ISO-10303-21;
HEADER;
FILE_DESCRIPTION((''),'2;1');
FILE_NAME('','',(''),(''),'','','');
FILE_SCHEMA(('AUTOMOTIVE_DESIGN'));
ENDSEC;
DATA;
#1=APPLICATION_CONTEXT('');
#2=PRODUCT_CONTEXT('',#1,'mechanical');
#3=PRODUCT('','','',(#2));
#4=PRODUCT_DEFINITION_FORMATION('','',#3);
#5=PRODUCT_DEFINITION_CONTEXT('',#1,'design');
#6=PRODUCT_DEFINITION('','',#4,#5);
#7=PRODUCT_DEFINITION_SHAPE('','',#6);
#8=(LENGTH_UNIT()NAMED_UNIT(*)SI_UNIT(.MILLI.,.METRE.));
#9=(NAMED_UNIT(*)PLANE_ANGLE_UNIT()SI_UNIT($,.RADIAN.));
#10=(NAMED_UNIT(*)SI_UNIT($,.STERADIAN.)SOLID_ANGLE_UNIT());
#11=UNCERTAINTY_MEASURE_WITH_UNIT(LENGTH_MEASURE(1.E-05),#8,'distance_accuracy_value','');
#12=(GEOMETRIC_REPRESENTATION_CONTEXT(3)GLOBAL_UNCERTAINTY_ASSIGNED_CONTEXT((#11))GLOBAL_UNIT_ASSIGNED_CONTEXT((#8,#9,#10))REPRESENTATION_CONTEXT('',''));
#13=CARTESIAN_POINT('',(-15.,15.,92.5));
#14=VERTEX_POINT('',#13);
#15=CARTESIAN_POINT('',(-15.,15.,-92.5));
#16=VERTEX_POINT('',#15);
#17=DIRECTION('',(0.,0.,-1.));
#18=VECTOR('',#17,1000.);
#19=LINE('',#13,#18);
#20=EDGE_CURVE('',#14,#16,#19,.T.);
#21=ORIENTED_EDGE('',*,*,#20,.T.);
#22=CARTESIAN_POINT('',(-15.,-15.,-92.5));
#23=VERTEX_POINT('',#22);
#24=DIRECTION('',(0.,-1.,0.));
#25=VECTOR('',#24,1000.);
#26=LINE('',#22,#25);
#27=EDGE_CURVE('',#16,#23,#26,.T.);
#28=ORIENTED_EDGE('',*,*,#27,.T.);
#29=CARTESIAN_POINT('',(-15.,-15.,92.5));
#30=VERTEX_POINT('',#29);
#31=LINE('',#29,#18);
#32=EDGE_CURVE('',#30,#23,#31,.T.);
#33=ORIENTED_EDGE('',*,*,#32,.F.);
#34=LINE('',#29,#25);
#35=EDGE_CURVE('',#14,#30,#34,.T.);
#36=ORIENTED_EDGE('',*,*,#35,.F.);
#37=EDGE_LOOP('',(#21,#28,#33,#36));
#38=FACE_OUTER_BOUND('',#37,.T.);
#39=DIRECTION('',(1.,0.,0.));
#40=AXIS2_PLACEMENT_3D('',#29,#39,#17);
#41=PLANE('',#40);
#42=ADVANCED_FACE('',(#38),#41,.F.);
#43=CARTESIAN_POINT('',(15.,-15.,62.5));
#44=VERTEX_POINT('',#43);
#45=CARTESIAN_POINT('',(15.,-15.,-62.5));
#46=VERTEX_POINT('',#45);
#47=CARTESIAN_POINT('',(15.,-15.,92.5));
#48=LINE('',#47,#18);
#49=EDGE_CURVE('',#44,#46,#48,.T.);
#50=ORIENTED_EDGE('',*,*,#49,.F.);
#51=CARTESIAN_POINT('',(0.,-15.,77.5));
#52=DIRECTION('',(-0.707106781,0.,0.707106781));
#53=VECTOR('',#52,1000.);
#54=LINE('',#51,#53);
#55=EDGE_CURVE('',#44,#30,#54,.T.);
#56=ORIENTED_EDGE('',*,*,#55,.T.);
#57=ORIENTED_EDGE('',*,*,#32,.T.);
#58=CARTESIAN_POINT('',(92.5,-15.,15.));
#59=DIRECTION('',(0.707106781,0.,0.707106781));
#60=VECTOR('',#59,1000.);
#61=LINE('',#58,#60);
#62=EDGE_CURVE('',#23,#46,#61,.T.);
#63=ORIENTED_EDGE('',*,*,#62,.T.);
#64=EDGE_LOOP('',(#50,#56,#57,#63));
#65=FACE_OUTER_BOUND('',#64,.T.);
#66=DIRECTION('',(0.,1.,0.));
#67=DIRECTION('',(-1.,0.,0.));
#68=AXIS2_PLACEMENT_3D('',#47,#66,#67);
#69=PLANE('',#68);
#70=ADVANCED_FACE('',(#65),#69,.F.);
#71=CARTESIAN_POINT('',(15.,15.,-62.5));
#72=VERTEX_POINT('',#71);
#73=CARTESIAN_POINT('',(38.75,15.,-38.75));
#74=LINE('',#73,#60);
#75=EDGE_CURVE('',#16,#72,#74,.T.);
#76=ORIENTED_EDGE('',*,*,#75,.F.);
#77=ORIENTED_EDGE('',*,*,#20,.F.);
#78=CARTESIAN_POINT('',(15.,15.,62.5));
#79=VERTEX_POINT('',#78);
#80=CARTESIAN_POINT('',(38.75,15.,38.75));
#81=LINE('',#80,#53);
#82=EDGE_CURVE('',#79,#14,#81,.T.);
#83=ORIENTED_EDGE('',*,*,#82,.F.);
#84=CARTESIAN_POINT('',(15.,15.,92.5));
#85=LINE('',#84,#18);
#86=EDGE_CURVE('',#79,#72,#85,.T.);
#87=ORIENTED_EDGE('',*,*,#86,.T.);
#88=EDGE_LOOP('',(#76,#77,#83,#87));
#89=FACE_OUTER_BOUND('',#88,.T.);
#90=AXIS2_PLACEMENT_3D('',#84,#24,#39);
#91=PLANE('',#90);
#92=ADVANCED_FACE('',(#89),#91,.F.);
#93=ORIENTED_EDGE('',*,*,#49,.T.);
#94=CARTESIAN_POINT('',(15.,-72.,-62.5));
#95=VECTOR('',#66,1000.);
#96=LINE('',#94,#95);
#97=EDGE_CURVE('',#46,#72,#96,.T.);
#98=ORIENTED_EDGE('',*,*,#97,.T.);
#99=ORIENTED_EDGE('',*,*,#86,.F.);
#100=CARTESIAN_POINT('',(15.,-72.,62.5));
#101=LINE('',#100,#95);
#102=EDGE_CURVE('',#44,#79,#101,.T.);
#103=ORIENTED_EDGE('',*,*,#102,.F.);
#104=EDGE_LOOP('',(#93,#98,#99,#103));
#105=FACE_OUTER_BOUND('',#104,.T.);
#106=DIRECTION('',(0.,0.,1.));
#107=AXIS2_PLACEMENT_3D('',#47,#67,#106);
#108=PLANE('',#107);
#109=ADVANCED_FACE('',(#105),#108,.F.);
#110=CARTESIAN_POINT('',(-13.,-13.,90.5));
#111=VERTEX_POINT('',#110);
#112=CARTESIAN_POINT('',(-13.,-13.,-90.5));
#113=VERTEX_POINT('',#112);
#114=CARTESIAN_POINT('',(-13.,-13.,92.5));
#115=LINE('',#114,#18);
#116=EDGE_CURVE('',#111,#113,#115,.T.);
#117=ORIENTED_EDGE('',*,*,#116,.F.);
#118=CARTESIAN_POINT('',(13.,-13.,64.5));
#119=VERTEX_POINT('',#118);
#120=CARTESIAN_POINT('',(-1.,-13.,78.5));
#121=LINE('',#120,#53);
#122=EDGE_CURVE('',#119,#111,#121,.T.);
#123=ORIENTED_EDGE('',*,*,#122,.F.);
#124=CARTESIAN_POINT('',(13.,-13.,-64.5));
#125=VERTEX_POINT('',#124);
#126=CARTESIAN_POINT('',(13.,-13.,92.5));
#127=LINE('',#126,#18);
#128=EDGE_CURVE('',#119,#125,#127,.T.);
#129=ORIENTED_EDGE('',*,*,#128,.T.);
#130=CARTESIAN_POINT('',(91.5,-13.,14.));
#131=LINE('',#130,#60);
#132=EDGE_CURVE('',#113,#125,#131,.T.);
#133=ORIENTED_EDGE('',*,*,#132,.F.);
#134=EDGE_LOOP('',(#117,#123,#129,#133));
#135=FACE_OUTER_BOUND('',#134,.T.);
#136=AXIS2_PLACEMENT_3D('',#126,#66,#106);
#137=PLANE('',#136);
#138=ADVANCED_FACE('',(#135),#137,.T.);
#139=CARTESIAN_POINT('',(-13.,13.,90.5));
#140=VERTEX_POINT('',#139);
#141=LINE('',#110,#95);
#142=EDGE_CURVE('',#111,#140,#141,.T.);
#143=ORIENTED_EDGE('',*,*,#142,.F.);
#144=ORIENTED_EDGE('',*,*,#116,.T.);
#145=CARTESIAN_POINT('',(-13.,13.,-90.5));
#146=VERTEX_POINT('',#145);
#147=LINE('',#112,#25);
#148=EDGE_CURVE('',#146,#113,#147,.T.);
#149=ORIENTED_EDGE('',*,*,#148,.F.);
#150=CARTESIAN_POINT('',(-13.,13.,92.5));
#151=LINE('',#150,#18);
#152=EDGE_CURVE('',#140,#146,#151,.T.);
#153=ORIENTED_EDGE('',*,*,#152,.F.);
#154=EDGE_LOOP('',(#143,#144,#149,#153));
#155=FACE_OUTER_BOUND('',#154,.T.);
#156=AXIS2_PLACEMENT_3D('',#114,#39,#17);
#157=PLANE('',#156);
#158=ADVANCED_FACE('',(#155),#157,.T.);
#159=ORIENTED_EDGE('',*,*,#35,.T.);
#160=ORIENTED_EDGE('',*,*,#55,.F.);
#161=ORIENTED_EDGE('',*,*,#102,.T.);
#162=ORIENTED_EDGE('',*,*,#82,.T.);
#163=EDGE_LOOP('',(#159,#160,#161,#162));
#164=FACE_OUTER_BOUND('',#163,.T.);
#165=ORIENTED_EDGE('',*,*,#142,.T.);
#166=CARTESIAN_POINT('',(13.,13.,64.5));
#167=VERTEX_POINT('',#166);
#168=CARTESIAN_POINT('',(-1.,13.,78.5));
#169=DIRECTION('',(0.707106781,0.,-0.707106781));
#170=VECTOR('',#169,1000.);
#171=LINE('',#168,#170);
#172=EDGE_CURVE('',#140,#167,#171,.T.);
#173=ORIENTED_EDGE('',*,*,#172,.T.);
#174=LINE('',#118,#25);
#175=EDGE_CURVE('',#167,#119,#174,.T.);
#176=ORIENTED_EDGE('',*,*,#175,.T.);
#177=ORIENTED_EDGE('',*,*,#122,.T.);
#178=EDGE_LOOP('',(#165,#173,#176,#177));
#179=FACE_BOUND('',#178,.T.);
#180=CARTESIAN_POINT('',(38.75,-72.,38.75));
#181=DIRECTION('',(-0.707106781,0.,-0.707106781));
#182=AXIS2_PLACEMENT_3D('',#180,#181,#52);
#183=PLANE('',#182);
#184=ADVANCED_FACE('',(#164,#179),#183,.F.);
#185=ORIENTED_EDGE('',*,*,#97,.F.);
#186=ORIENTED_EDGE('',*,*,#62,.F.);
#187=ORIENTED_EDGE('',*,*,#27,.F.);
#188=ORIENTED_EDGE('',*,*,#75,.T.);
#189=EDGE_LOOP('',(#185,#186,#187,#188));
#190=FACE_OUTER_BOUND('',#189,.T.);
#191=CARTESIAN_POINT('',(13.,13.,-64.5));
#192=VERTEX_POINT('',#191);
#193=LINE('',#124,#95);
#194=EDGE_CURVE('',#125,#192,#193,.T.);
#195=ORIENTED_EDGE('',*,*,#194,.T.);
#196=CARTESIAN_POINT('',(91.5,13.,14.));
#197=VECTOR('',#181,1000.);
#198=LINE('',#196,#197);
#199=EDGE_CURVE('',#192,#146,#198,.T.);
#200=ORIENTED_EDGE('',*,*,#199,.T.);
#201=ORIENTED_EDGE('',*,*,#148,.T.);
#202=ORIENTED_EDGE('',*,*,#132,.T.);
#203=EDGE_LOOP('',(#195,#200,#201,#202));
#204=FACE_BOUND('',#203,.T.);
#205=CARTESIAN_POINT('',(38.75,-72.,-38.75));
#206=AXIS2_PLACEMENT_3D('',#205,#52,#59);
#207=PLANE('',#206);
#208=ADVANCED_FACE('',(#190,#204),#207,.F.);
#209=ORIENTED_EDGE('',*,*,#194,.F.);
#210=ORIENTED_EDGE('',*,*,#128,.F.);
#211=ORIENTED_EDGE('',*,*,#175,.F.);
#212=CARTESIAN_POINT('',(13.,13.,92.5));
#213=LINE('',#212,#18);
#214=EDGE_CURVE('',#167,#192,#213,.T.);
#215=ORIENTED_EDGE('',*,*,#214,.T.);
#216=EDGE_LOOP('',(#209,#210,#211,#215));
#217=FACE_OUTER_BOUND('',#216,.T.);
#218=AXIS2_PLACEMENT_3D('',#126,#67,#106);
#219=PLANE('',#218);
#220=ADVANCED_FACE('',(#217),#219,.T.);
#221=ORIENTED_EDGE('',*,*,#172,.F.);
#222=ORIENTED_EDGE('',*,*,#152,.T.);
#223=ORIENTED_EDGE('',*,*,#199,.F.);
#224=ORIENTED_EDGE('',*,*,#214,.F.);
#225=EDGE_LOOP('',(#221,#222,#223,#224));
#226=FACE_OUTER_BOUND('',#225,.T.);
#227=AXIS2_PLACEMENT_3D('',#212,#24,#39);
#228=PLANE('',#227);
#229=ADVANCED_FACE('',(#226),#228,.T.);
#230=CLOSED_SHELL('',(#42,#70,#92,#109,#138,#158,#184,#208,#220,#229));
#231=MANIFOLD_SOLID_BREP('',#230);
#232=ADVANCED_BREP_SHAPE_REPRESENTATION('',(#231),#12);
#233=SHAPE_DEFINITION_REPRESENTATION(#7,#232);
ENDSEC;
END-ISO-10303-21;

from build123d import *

# Parameters (mm, degrees)
SKETCH_1_W          = 30
SKETCH_1_H          = 30
SKETCH_1_W_2        = 26
SKETCH_1_H_2        = 26
EXTRUDE_1_DEPTH     = 92.5
CUT_EXTRUDE_1_DEPTH = 87


with BuildPart() as part:
    # 草图1 → 凸台-拉伸1 (new, symmetric)
    with BuildSketch(Plane.XY):
        Rectangle(SKETCH_1_W, SKETCH_1_H)
        Rectangle(SKETCH_1_W_2, SKETCH_1_H_2, mode=Mode.SUBTRACT)
    extrude(amount=EXTRUDE_1_DEPTH, both=True)

    # 草图2 → 切除-拉伸1 (cut)
    with BuildSketch(Plane(origin=(0, 15, 0), x_dir=(1, 0, 0), z_dir=(0, 1, 0))):
        Polygon((15, -62.5), (-15, -92.5), (15, -92.5), align=None)
        Polygon((15, 92.5), (-15, 92.5), (15, 62.5), align=None)
    extrude(amount=-CUT_EXTRUDE_1_DEPTH, mode=Mode.SUBTRACT)


solid = part.part
